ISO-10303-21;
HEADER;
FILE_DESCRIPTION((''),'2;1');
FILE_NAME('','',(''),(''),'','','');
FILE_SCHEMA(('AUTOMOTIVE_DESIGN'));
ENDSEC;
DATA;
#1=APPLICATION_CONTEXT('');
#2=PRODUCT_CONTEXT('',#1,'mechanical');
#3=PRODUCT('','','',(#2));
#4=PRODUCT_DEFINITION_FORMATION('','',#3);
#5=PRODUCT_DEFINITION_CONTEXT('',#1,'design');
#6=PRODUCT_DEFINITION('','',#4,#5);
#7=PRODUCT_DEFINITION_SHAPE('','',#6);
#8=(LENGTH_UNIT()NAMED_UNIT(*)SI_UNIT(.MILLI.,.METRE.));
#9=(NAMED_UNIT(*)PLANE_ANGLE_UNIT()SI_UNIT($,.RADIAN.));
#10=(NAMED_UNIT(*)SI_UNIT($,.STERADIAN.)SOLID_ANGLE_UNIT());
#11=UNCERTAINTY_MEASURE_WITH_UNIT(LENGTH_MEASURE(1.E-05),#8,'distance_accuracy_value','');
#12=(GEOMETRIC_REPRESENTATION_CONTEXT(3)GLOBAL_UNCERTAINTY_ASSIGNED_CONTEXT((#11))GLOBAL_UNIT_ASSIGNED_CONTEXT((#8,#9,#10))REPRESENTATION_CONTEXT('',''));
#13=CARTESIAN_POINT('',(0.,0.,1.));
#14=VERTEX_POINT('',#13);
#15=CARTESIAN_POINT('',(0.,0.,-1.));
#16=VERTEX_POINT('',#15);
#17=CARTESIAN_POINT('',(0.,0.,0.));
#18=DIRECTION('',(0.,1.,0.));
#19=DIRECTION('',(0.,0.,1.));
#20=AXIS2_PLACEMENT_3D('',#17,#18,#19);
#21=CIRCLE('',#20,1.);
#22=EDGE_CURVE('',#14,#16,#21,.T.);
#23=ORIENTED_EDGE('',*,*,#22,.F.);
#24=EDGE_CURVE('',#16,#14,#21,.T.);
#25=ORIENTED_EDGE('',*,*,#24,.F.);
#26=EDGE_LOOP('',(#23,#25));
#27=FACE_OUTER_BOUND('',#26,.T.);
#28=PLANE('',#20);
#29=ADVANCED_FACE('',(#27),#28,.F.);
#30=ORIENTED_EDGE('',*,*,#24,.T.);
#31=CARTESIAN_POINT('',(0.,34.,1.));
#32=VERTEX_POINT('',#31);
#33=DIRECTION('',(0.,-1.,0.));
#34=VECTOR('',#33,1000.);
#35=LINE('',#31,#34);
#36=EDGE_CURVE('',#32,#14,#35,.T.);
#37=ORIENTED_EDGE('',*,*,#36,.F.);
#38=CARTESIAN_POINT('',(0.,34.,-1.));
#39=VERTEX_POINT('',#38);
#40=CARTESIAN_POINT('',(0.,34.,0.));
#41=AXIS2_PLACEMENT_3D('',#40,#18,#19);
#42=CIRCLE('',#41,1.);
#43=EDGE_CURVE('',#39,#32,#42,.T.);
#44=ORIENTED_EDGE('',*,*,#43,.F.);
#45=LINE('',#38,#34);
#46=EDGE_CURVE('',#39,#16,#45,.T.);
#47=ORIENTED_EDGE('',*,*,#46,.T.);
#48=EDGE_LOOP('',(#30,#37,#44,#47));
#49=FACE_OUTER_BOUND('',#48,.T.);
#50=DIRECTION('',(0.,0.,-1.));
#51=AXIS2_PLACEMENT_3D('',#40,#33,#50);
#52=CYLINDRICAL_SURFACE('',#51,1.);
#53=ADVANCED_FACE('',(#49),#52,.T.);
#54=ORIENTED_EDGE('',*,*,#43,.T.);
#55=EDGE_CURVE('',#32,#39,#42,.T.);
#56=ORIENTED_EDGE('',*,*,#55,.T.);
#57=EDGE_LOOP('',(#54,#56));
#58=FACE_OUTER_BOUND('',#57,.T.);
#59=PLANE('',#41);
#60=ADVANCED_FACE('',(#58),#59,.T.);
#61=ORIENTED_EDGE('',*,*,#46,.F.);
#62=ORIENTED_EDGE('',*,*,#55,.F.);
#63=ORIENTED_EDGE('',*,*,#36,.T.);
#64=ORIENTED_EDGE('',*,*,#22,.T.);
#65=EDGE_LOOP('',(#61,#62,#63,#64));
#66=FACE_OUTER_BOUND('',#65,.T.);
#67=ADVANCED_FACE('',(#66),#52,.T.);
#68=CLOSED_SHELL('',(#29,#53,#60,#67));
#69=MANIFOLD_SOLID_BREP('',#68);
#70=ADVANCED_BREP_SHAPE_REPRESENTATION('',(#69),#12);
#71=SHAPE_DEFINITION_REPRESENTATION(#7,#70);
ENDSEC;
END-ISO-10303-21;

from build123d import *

# Parameters (mm, degrees)
SKETCH_1_R      = 1
EXTRUDE_1_DEPTH = 34


with BuildPart() as part:
    # 草图1 → 凸台-拉伸1 (new body)
    with BuildSketch(Plane(origin=(0, 0, 0), x_dir=(1, 0, 0), z_dir=(0, 1, 0))):
        with Locations(Location((0, 0, 0), (0, 0, 270))):
            Circle(SKETCH_1_R)
    extrude(amount=EXTRUDE_1_DEPTH)


solid = part.part
